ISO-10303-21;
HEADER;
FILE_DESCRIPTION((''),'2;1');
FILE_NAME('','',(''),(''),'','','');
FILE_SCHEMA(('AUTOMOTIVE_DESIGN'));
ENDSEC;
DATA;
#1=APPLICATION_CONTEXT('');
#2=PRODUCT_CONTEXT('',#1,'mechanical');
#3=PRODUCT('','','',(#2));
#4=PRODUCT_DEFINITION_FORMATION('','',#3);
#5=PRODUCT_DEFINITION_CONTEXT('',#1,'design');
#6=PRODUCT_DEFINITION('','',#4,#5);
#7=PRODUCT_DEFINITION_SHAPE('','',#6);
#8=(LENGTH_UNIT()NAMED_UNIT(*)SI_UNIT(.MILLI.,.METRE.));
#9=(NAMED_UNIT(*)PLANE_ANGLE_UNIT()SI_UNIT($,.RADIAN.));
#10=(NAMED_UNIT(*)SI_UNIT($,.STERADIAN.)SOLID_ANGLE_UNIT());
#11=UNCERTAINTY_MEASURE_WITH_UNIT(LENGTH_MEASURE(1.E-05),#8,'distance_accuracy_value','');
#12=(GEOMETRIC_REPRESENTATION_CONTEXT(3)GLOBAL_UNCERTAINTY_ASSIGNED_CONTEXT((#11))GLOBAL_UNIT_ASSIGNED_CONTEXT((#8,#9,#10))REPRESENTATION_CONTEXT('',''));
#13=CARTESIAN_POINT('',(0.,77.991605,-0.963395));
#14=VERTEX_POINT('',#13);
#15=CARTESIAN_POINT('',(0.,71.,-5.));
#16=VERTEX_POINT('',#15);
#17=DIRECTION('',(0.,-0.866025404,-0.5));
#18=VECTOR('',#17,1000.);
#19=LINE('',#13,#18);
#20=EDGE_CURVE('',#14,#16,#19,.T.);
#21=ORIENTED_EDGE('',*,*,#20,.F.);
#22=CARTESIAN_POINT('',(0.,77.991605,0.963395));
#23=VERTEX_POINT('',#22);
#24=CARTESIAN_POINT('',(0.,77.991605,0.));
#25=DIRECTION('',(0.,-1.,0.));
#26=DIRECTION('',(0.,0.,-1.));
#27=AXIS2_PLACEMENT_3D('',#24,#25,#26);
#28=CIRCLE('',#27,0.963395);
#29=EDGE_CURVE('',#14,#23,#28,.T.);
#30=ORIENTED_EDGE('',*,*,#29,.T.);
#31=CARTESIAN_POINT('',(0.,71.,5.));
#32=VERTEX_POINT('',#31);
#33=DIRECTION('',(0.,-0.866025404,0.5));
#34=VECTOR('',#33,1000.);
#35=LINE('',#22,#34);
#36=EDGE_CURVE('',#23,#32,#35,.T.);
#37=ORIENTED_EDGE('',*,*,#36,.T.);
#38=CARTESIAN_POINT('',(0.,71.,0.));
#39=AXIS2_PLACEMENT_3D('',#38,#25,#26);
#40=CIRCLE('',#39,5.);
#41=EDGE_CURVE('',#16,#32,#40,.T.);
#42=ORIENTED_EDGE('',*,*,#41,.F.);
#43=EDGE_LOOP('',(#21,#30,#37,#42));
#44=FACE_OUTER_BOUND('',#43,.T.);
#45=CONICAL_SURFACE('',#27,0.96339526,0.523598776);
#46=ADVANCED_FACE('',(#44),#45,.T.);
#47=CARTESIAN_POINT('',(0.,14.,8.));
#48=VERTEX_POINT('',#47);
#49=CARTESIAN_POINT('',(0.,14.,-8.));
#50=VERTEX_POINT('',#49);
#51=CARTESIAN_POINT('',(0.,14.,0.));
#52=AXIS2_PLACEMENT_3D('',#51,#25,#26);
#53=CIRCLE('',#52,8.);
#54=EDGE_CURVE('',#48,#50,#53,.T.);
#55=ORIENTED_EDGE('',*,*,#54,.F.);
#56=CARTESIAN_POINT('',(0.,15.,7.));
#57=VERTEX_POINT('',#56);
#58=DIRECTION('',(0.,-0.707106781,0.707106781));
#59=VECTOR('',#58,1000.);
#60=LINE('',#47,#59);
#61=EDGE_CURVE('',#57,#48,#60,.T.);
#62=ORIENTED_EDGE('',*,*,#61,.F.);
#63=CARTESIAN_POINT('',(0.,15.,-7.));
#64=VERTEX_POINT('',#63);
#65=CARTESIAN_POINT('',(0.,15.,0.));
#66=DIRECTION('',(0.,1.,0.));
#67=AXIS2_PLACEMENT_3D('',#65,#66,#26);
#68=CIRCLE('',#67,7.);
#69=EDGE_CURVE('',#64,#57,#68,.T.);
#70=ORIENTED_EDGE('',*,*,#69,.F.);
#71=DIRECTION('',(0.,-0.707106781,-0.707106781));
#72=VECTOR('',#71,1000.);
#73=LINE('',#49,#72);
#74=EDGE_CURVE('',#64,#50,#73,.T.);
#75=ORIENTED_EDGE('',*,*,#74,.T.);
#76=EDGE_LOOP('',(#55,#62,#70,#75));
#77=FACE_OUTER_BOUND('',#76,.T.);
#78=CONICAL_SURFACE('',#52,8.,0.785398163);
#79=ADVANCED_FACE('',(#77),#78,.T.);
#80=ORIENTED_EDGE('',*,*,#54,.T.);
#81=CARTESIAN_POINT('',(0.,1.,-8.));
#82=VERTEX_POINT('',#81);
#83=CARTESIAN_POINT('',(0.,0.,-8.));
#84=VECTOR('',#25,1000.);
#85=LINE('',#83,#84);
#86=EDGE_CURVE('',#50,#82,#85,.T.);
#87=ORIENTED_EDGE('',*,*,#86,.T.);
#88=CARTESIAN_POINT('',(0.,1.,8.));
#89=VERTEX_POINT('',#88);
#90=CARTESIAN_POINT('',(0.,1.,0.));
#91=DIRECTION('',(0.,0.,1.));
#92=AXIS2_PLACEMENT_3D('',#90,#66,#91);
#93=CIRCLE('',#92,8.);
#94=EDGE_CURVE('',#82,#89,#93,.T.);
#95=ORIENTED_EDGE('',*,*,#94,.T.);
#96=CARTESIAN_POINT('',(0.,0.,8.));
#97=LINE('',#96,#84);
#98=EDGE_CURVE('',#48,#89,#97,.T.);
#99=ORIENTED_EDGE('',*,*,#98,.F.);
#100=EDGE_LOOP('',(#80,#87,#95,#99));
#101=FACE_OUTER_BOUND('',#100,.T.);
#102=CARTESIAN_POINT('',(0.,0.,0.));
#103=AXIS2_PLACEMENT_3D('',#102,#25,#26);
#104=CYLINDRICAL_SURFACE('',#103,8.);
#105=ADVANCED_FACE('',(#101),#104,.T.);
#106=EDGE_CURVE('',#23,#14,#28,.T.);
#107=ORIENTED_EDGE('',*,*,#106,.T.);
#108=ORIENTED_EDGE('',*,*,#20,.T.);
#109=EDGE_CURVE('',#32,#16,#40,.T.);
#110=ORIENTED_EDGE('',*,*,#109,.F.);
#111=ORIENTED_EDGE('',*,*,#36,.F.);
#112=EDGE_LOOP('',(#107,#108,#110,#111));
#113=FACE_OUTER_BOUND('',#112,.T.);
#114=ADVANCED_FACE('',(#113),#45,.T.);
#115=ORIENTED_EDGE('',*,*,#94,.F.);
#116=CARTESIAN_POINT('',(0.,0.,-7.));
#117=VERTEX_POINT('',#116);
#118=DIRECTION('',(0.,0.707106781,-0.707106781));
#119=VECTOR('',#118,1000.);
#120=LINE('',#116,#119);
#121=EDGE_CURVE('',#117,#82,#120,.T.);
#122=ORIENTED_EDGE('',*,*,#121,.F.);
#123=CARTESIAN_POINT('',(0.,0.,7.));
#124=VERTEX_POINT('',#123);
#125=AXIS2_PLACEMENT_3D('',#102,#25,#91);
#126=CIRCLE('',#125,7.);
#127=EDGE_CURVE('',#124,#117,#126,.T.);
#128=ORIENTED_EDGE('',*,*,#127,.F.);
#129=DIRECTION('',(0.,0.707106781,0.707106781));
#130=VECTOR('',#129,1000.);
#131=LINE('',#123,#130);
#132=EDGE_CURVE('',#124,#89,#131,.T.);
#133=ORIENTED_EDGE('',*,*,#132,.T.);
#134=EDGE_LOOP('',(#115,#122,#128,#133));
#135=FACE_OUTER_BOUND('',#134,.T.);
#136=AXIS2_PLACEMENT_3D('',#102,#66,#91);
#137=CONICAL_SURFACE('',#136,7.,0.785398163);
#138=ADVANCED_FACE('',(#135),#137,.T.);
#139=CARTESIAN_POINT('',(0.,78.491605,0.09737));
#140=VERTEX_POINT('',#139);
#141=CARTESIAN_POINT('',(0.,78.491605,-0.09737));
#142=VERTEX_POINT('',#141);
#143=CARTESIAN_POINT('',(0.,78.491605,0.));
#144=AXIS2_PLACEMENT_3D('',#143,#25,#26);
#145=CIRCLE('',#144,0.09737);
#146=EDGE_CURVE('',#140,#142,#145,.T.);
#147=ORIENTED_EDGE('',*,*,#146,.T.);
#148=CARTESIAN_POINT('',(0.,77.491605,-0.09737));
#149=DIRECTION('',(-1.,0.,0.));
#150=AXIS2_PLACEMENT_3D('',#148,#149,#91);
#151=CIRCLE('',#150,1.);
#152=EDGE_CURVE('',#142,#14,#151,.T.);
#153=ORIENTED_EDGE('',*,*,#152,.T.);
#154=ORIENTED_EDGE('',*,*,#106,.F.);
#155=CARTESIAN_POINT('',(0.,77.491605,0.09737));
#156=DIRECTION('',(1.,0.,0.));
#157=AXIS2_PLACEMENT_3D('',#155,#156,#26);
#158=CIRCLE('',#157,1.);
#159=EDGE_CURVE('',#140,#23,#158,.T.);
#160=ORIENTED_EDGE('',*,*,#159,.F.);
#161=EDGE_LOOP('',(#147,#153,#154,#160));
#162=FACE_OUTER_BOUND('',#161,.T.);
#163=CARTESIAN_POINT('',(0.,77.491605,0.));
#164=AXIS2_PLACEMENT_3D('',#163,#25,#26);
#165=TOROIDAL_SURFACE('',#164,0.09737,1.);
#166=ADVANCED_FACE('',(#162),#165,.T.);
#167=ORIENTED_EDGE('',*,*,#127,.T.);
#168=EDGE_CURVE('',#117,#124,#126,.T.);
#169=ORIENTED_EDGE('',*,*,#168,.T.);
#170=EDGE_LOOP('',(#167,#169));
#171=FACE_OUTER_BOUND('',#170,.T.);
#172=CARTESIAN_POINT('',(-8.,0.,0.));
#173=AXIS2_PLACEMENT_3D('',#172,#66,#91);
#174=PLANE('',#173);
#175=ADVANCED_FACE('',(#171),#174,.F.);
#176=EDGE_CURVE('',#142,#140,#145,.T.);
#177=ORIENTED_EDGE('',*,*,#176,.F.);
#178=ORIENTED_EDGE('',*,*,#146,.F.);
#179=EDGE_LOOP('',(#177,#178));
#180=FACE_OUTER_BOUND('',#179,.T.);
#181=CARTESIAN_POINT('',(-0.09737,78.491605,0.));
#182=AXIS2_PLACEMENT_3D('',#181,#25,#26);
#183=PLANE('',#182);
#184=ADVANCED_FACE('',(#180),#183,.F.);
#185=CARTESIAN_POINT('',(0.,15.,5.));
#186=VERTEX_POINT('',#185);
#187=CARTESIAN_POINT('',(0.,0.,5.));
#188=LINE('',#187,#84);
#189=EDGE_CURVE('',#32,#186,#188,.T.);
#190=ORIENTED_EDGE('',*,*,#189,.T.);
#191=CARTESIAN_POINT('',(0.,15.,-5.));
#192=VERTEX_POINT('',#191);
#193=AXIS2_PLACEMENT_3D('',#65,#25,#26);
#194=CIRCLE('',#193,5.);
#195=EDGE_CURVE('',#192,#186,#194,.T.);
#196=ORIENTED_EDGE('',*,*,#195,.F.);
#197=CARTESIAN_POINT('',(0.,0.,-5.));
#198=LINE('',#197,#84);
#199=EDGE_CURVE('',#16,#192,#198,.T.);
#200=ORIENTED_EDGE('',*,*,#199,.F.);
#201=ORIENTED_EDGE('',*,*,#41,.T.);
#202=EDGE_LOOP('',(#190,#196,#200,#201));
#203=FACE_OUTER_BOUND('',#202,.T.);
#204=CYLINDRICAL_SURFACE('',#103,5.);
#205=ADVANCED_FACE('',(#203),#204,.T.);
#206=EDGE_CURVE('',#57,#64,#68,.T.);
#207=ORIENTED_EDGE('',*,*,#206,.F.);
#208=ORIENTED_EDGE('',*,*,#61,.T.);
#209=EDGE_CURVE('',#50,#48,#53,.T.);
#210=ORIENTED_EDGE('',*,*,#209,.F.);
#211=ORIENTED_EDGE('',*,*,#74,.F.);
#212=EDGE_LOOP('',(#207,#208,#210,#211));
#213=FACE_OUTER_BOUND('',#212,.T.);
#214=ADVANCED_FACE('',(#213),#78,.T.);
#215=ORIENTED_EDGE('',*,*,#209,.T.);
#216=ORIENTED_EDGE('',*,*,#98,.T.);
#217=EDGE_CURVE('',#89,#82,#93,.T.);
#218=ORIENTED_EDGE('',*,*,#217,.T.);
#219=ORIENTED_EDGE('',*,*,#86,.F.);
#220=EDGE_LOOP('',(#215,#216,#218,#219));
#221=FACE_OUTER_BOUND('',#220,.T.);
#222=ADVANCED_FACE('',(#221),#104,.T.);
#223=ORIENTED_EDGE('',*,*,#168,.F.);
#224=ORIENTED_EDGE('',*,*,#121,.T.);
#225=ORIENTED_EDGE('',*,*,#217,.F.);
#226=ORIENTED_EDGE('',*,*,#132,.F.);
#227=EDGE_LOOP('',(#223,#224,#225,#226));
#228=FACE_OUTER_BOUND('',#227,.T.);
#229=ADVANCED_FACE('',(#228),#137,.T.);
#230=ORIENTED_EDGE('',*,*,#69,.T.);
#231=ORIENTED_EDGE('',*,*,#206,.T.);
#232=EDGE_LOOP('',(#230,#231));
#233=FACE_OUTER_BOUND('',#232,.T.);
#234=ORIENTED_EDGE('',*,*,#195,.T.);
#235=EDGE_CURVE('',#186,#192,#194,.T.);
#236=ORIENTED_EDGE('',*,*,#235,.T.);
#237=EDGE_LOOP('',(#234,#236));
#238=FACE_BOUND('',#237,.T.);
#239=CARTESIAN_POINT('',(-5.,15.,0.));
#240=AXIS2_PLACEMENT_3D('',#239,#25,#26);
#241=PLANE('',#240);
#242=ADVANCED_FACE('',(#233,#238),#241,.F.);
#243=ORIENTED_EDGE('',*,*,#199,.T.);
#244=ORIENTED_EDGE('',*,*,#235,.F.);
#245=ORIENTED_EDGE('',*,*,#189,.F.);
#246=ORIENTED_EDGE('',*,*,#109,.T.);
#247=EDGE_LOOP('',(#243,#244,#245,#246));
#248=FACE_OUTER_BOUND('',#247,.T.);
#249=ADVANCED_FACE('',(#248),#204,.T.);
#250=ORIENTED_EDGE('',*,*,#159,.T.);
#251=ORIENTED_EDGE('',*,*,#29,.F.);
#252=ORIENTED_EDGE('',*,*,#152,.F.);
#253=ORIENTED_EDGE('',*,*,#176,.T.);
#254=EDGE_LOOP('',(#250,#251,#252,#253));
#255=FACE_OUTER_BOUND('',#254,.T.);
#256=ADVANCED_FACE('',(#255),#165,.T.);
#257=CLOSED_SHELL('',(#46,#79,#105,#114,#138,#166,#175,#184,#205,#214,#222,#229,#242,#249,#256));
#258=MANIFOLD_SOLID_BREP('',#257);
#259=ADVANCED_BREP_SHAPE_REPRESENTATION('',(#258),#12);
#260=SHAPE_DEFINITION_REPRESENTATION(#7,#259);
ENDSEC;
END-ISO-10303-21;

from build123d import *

# Parameters (mm, degrees)
CHAMFER1_SIZE = 1


with BuildPart() as part:
    # Sketch1 → Revolve1 (revolve)
    with BuildSketch(Plane.XY, mode=Mode.PRIVATE) as revolve1_sk:
        with BuildLine():
            Line((-0.96339526, 77.991604501), (-5, 71))
            Line((-5, 71), (-5, 15))
            Line((-5, 15), (-8, 15))
            Line((-8, 15), (-8, 0))
            Line((-8, 0), (0, 0))
            Line((0, 0), (0, 78.491604501))
            Line((0, 78.491604501), (-0.097369856, 78.491604501))
            ThreePointArc((-0.097369856, 78.491604501), (-0.597369856, 78.357629904), (-0.96339526, 77.991604501))
        make_face()
    revolve(revolve1_sk.sketch.rotate(Axis((0, 0, 0), (0, 1, 0)), 270), axis=Axis((0, 0, 0), (0, 1, 0)))

    # Chamfer1
    chamfer1_edges = [part.edges().sort_by_distance(p)[0] for p in [
        (0, 0, 8),
        (0, 15, 8),
    ]]
    chamfer(chamfer1_edges, length=CHAMFER1_SIZE)


solid = part.part
